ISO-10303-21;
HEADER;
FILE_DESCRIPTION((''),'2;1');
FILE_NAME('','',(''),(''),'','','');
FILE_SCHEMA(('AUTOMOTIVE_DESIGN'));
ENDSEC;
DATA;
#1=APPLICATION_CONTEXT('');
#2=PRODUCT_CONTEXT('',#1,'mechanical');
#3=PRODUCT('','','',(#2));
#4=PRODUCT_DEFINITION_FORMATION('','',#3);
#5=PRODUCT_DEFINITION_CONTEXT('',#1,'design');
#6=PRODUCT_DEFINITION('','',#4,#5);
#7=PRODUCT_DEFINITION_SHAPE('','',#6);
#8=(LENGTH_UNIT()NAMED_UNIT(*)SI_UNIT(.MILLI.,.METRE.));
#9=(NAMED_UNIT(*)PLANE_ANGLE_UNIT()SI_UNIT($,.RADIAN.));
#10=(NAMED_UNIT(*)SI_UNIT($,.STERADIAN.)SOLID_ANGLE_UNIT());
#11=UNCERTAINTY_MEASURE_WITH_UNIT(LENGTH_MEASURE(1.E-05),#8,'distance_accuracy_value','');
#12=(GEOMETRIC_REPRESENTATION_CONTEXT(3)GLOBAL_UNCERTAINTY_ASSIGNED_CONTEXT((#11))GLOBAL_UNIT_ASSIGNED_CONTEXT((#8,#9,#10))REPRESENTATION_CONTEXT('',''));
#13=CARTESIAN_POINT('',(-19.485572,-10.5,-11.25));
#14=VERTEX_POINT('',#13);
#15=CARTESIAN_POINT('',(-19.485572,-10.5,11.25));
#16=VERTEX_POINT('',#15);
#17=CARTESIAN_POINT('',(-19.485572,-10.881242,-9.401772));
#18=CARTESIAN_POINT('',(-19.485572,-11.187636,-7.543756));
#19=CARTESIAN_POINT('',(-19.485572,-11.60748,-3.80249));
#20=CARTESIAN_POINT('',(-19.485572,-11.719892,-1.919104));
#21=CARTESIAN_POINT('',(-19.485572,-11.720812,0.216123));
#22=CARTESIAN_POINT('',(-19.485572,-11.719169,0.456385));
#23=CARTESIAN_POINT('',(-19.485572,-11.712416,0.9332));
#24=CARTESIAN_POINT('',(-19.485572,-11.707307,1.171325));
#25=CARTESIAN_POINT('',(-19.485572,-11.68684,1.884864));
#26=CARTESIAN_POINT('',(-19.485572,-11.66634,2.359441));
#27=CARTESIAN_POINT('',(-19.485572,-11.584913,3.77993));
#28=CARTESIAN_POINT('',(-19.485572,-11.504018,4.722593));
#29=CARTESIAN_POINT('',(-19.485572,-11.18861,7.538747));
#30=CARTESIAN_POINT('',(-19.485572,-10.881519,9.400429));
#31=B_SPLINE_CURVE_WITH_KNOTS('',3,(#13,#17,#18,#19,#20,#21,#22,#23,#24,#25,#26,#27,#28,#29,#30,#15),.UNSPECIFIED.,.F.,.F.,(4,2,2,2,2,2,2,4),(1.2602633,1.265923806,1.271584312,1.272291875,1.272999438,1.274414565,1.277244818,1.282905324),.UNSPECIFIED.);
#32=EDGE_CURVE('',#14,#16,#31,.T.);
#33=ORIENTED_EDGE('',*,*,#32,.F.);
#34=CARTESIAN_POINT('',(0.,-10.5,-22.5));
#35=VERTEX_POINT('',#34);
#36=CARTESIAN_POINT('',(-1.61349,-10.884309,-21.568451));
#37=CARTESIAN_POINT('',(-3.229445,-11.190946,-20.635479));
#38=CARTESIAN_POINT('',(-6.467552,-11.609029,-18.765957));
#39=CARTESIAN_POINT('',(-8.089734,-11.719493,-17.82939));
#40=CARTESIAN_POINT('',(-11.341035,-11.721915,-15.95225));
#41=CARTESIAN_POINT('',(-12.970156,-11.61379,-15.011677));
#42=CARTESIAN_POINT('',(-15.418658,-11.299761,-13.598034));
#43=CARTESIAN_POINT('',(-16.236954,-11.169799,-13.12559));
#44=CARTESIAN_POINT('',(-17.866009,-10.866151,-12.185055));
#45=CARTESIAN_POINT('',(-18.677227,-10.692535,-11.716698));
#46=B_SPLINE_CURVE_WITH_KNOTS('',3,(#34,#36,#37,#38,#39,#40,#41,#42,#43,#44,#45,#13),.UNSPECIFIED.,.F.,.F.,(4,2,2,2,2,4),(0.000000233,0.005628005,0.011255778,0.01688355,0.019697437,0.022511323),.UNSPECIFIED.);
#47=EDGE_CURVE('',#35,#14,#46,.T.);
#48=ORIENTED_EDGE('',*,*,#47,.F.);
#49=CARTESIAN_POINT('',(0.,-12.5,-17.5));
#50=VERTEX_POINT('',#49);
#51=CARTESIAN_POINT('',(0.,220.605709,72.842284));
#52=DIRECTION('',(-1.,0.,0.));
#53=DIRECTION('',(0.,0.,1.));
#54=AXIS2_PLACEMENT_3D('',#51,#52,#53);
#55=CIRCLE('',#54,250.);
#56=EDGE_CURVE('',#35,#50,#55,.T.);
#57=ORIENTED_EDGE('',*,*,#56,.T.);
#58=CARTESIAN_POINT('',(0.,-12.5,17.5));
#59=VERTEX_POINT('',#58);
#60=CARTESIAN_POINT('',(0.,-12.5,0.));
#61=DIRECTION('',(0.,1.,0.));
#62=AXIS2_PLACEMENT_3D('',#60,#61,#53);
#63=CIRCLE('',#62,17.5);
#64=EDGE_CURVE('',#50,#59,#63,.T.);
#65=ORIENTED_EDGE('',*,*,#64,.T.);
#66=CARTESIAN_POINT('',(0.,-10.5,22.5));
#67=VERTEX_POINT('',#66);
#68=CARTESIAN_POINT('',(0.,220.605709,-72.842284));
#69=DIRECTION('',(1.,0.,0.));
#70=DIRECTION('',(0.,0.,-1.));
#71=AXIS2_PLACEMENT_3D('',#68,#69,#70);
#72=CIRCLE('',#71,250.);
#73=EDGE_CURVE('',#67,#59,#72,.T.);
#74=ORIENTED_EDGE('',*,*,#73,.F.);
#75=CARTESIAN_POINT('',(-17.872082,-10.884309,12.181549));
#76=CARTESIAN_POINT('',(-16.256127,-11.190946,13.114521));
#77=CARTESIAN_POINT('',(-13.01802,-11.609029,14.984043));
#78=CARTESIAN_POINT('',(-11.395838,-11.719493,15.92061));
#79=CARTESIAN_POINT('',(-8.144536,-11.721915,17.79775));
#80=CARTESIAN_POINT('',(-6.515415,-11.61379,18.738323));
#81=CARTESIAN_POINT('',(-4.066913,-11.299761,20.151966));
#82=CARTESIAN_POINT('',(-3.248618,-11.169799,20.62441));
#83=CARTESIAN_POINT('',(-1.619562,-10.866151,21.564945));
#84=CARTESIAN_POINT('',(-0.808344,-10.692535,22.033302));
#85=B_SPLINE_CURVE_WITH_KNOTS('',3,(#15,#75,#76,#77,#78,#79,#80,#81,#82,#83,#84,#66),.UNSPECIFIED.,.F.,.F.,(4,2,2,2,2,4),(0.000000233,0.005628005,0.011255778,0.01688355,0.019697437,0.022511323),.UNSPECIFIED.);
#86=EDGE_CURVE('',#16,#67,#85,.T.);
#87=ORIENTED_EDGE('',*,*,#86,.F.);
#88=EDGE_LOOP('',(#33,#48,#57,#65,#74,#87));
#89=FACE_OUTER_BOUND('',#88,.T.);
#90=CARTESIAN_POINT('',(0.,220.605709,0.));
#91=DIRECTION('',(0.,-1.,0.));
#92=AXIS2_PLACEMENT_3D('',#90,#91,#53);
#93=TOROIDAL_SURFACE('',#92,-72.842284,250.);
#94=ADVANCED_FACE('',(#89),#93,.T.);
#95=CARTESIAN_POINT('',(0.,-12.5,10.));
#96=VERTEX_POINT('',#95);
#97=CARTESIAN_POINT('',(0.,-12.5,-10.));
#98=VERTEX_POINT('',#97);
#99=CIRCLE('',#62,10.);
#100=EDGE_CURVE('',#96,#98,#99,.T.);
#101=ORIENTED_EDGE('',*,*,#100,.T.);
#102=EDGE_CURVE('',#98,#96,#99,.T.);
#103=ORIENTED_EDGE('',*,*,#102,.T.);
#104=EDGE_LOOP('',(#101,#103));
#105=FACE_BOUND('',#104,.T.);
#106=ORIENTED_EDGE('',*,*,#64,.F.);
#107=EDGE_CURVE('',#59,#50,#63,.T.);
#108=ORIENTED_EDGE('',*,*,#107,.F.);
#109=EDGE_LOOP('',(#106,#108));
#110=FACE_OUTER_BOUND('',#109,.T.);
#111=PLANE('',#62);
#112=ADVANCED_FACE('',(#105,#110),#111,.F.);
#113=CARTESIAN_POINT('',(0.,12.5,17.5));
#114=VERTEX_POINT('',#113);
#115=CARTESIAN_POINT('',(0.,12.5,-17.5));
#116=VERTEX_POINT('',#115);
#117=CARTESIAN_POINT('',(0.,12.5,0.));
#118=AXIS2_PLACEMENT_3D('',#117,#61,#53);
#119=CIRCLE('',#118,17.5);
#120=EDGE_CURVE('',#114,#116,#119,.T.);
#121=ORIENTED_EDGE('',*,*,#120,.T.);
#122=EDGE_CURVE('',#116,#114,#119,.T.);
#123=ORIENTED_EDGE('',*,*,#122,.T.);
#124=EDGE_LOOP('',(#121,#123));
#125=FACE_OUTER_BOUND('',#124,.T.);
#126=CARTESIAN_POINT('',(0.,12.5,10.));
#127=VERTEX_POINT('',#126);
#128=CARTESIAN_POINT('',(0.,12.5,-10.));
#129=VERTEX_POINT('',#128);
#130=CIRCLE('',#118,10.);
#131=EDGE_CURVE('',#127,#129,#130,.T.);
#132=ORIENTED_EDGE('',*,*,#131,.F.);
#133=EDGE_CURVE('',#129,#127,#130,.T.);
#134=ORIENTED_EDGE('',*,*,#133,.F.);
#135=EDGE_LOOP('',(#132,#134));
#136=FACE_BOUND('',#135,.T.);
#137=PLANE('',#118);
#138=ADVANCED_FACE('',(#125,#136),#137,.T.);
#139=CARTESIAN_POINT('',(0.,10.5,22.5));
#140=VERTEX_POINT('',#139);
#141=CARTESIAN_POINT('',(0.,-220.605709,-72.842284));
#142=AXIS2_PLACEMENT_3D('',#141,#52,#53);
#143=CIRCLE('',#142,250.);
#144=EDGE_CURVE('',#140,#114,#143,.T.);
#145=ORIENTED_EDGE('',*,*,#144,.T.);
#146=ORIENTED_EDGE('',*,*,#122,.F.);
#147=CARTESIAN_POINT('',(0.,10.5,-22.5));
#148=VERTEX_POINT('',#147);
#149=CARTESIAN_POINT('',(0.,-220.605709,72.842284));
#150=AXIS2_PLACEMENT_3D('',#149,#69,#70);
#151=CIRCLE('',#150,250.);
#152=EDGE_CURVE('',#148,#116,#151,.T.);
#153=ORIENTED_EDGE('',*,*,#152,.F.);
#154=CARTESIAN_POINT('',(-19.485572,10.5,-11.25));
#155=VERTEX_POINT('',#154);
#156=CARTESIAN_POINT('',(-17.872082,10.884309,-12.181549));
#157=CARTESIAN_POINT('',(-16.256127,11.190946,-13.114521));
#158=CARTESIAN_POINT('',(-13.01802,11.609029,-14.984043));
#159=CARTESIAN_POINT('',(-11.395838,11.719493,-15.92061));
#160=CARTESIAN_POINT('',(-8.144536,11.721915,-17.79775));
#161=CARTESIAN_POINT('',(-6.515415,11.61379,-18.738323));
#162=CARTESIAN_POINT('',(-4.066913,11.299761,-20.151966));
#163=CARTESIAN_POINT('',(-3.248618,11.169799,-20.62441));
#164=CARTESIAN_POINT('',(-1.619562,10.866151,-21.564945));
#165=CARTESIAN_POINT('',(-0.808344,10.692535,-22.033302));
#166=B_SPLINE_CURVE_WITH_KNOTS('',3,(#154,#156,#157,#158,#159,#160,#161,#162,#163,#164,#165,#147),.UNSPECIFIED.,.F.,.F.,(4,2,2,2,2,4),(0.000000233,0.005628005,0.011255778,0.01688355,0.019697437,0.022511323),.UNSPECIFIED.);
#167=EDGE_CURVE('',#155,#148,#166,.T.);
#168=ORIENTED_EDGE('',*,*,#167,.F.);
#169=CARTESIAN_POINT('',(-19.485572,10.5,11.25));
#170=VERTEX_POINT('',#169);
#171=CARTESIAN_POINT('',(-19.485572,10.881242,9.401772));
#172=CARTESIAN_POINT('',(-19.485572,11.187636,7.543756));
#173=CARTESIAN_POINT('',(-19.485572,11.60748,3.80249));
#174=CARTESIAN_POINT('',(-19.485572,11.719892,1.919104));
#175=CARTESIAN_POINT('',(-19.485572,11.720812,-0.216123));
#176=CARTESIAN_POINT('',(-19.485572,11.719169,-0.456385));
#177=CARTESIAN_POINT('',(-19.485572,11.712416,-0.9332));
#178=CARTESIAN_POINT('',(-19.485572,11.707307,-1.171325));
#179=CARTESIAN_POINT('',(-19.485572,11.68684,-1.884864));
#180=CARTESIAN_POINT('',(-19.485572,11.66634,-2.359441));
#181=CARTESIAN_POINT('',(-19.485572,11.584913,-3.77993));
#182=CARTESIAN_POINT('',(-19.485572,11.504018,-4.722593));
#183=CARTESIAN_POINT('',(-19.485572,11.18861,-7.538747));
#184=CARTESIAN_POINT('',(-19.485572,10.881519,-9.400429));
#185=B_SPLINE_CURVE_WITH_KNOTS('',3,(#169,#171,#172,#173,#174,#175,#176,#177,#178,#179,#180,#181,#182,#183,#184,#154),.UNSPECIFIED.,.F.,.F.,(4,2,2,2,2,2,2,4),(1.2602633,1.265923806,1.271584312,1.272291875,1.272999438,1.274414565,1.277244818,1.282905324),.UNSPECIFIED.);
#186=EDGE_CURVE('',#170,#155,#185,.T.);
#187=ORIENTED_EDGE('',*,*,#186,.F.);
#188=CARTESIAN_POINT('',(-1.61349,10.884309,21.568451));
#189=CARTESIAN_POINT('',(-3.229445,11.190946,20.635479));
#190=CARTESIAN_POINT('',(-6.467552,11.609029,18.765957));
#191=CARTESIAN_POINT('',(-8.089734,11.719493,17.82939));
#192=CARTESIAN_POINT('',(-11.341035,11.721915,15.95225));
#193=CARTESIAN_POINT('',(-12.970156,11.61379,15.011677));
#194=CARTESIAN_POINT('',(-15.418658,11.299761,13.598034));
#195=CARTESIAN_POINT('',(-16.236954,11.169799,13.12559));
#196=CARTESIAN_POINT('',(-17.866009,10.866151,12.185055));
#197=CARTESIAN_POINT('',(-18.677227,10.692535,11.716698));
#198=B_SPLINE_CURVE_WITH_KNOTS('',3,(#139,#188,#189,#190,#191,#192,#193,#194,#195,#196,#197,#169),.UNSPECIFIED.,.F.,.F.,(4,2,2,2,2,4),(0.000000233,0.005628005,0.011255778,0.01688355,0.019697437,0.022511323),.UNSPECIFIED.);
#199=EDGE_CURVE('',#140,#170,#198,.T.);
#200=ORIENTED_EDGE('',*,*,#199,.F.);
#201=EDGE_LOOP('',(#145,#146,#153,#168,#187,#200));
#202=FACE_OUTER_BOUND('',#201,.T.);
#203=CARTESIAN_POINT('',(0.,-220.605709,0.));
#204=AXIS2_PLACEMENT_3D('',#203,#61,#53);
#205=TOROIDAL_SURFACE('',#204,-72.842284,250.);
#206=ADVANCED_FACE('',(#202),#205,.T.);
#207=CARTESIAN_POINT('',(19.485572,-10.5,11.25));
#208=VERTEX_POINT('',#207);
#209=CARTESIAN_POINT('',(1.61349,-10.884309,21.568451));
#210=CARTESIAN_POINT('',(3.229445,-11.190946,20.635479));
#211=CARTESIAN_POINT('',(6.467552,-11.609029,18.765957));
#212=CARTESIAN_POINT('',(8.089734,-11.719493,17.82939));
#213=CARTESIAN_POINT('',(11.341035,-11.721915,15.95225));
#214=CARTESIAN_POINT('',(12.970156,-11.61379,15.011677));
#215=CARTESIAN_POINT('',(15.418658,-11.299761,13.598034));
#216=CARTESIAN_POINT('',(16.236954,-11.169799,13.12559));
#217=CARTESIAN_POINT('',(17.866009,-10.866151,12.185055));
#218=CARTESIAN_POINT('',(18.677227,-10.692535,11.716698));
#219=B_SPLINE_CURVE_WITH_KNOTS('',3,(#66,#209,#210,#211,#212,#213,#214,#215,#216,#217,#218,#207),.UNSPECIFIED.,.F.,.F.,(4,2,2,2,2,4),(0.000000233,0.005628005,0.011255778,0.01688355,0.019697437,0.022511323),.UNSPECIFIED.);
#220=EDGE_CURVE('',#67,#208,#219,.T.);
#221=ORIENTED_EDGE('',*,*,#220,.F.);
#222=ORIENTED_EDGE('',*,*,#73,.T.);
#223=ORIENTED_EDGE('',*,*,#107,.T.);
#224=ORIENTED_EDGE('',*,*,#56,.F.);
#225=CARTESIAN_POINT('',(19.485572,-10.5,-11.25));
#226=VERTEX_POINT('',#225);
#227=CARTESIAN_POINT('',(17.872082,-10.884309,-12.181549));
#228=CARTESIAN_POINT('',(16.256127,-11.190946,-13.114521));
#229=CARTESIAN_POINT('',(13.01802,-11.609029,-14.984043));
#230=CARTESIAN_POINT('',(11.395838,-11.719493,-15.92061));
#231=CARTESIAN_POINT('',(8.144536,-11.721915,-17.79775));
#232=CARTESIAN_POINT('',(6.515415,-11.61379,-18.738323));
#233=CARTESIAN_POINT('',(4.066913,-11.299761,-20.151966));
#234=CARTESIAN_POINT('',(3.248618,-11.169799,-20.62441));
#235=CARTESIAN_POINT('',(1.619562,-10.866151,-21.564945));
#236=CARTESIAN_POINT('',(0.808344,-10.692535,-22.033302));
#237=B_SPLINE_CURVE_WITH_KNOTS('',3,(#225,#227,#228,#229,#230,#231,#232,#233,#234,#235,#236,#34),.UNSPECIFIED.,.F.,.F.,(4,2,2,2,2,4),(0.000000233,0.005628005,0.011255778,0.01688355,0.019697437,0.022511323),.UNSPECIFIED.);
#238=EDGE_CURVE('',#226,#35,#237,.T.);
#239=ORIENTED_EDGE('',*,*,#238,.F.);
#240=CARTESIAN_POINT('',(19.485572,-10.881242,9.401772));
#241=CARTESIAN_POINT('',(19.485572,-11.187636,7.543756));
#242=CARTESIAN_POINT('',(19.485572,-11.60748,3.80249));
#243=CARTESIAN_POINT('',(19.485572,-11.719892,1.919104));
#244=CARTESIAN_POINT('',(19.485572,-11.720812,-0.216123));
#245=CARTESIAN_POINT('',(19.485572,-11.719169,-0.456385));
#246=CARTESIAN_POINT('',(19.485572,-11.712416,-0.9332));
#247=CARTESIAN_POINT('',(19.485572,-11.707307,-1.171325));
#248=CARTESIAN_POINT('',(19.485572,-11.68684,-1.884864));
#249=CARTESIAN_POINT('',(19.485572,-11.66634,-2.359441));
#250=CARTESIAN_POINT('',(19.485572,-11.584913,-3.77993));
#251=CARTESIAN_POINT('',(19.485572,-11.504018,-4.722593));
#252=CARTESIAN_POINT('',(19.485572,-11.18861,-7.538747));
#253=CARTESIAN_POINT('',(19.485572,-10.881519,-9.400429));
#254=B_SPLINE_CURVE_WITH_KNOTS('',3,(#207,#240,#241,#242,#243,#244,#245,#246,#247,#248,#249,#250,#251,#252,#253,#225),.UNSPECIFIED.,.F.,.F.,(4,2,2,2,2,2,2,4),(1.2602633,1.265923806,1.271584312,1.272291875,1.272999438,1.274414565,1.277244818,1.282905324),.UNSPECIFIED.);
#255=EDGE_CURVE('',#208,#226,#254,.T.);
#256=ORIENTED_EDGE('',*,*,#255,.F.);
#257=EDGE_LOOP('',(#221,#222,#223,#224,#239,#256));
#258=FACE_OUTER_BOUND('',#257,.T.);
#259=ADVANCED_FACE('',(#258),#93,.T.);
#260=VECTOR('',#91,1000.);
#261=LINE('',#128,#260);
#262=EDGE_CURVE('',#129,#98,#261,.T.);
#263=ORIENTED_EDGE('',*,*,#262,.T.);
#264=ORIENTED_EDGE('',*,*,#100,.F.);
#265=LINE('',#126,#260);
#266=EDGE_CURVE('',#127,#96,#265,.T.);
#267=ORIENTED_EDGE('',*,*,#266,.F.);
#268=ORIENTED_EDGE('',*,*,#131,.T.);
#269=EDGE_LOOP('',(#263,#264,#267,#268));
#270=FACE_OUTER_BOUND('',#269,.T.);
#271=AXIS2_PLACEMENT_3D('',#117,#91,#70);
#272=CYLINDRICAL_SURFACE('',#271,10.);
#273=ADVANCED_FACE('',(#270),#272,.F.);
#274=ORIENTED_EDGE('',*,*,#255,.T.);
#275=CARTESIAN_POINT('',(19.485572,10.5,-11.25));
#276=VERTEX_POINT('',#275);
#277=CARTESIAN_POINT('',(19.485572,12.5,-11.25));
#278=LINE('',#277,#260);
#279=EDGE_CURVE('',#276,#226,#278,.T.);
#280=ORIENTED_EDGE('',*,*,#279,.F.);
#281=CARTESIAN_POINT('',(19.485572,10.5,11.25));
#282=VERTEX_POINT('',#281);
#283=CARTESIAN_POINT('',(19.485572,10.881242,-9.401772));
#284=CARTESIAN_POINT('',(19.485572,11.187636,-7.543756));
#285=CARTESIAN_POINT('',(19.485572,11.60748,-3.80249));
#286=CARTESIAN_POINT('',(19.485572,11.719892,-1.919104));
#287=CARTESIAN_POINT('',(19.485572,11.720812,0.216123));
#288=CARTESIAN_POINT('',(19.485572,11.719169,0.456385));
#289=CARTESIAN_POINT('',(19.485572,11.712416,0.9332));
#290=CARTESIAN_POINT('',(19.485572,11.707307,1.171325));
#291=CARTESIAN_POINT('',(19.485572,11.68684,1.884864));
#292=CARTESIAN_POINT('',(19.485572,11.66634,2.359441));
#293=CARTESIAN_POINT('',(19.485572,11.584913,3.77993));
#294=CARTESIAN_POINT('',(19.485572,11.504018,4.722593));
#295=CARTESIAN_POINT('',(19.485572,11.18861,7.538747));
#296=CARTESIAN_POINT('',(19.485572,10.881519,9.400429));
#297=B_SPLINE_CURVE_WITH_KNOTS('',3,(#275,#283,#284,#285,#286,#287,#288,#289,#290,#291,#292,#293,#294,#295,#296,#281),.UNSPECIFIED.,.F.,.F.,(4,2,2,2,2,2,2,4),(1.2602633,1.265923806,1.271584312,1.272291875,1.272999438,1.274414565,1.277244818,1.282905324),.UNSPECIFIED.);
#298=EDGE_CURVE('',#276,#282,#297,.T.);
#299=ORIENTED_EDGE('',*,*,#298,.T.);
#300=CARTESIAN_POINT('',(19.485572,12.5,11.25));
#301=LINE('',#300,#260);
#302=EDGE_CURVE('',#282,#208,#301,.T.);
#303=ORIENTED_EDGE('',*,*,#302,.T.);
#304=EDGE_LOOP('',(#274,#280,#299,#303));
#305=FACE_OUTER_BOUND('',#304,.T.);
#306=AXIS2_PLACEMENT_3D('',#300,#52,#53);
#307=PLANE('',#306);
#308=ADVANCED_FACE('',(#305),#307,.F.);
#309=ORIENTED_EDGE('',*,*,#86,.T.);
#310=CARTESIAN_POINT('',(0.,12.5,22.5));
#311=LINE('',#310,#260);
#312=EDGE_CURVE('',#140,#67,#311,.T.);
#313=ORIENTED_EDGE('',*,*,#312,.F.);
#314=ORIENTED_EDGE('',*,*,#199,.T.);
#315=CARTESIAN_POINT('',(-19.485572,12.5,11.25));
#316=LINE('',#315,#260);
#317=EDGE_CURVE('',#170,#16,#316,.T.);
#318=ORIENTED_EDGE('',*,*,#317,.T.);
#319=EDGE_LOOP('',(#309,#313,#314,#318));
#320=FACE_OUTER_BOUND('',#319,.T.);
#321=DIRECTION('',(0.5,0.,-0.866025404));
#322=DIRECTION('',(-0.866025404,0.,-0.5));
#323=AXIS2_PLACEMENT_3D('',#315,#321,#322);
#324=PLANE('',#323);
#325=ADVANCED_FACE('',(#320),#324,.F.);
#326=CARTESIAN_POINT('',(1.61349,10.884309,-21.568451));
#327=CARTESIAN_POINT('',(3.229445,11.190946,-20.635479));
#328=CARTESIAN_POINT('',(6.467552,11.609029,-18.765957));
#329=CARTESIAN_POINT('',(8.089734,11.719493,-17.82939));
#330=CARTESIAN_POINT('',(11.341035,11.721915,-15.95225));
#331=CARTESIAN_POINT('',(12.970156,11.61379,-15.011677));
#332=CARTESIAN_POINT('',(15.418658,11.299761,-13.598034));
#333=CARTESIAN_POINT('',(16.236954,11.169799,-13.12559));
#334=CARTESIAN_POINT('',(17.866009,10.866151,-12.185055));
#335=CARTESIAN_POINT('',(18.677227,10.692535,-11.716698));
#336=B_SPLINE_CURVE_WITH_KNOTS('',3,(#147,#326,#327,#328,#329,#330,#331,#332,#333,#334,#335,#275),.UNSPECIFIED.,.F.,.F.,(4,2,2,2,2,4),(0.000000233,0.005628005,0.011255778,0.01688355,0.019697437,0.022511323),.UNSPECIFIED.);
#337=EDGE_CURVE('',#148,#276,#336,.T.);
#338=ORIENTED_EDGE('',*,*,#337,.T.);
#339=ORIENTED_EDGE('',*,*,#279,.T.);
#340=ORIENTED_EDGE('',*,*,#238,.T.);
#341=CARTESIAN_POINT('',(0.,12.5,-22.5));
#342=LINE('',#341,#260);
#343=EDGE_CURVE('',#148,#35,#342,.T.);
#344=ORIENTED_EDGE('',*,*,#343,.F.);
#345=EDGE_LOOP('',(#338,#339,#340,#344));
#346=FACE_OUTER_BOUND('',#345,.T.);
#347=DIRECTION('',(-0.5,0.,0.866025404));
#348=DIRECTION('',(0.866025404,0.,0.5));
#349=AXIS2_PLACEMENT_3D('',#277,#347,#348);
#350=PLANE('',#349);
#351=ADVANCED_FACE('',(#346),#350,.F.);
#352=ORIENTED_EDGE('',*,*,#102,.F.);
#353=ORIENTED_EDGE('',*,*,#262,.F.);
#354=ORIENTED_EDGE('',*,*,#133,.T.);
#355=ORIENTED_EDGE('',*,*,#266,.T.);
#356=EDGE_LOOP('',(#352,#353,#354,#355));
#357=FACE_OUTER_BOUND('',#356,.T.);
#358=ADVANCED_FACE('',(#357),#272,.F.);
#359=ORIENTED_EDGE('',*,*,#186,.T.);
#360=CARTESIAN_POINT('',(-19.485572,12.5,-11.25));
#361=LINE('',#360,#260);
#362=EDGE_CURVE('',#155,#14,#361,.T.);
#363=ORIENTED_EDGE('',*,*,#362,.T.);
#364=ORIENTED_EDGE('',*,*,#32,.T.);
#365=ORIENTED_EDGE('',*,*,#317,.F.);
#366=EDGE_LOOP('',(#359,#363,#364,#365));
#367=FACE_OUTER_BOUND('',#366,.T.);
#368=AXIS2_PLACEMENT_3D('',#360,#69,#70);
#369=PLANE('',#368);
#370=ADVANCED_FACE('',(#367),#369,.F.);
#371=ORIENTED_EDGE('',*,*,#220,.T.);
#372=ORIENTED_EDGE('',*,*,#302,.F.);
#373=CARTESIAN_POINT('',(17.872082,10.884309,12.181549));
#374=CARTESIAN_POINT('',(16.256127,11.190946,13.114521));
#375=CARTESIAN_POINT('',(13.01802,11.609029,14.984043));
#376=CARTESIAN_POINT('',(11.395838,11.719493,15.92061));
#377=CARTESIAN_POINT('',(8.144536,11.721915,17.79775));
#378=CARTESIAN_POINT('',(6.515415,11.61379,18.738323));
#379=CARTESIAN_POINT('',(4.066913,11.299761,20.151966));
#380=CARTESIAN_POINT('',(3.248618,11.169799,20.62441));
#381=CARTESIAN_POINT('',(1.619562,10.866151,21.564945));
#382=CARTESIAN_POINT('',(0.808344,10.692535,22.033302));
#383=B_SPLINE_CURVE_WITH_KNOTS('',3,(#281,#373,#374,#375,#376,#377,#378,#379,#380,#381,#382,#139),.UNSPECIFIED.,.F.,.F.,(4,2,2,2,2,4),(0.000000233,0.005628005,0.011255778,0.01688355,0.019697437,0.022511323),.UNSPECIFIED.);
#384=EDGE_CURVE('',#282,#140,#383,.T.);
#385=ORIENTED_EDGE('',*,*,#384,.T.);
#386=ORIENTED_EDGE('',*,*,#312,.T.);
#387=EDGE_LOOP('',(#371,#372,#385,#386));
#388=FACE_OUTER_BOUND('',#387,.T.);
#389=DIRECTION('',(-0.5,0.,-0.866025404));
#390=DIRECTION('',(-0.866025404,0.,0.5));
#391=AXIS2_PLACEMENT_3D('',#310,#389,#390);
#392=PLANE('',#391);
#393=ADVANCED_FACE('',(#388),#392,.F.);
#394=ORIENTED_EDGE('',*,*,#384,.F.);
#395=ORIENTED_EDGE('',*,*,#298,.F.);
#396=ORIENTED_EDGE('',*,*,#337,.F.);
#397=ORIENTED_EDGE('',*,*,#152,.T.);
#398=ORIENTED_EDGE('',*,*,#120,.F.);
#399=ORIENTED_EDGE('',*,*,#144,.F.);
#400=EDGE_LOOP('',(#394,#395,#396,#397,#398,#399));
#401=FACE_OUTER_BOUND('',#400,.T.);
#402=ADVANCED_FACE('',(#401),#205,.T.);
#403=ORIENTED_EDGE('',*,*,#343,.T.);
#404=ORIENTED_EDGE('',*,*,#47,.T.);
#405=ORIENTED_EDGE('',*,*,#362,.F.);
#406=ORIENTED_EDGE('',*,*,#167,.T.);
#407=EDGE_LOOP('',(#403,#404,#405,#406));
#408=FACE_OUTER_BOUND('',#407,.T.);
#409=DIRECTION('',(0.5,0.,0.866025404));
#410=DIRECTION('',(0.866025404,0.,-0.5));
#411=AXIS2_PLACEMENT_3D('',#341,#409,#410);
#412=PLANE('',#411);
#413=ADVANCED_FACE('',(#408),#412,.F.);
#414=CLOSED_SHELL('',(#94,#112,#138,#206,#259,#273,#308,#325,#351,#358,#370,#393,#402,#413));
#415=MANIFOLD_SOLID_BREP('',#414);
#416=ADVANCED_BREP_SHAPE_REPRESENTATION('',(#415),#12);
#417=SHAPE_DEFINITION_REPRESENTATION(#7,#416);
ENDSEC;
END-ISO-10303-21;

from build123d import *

# Parameters (mm, degrees)
SKETCH_1_R      = 10
EXTRUDE_1_DEPTH = 12.5


with BuildPart() as part:
    # 草图1 → 凸台-拉伸1 (new, symmetric)
    with BuildSketch(Plane(origin=(0, 0, 0), x_dir=(1, 0, 0), z_dir=(0, 1, 0))):
        Polygon((0, 22.5), (-19.485571585, 11.25), (-19.485571585, -11.25), (0, -22.5), (19.485571585, -11.25), (19.485571585, 11.25), align=None)
        with Locations(Location((0, 0, 0), (0, 0, 270))):
            Circle(SKETCH_1_R, mode=Mode.SUBTRACT)
    extrude(amount=EXTRUDE_1_DEPTH, both=True)

    # 草图2 → 切除-旋转1 (revolve, cut)
    with BuildSketch(Plane(origin=(0, 0, 0), x_dir=(0, 0, -1), z_dir=(1, 0, 0))):
        with BuildLine():
            Line((-22.5, 10.5), (-22.5, 12.5))
            Line((-22.5, 12.5), (-17.5, 12.5))
            ThreePointArc((-17.5, 12.5), (-20.005385321, 11.513463302), (-22.5, 10.5))
        make_face()
    cut_revolve_1 = revolve(axis=Axis((0, 32.499694269, 0), (0, -1, 0)), mode=Mode.SUBTRACT)

    # 镜向1: 切除-旋转1 across plane
    add(cut_revolve_1.mirror(Plane.ZX), mode=Mode.SUBTRACT)


solid = part.part
